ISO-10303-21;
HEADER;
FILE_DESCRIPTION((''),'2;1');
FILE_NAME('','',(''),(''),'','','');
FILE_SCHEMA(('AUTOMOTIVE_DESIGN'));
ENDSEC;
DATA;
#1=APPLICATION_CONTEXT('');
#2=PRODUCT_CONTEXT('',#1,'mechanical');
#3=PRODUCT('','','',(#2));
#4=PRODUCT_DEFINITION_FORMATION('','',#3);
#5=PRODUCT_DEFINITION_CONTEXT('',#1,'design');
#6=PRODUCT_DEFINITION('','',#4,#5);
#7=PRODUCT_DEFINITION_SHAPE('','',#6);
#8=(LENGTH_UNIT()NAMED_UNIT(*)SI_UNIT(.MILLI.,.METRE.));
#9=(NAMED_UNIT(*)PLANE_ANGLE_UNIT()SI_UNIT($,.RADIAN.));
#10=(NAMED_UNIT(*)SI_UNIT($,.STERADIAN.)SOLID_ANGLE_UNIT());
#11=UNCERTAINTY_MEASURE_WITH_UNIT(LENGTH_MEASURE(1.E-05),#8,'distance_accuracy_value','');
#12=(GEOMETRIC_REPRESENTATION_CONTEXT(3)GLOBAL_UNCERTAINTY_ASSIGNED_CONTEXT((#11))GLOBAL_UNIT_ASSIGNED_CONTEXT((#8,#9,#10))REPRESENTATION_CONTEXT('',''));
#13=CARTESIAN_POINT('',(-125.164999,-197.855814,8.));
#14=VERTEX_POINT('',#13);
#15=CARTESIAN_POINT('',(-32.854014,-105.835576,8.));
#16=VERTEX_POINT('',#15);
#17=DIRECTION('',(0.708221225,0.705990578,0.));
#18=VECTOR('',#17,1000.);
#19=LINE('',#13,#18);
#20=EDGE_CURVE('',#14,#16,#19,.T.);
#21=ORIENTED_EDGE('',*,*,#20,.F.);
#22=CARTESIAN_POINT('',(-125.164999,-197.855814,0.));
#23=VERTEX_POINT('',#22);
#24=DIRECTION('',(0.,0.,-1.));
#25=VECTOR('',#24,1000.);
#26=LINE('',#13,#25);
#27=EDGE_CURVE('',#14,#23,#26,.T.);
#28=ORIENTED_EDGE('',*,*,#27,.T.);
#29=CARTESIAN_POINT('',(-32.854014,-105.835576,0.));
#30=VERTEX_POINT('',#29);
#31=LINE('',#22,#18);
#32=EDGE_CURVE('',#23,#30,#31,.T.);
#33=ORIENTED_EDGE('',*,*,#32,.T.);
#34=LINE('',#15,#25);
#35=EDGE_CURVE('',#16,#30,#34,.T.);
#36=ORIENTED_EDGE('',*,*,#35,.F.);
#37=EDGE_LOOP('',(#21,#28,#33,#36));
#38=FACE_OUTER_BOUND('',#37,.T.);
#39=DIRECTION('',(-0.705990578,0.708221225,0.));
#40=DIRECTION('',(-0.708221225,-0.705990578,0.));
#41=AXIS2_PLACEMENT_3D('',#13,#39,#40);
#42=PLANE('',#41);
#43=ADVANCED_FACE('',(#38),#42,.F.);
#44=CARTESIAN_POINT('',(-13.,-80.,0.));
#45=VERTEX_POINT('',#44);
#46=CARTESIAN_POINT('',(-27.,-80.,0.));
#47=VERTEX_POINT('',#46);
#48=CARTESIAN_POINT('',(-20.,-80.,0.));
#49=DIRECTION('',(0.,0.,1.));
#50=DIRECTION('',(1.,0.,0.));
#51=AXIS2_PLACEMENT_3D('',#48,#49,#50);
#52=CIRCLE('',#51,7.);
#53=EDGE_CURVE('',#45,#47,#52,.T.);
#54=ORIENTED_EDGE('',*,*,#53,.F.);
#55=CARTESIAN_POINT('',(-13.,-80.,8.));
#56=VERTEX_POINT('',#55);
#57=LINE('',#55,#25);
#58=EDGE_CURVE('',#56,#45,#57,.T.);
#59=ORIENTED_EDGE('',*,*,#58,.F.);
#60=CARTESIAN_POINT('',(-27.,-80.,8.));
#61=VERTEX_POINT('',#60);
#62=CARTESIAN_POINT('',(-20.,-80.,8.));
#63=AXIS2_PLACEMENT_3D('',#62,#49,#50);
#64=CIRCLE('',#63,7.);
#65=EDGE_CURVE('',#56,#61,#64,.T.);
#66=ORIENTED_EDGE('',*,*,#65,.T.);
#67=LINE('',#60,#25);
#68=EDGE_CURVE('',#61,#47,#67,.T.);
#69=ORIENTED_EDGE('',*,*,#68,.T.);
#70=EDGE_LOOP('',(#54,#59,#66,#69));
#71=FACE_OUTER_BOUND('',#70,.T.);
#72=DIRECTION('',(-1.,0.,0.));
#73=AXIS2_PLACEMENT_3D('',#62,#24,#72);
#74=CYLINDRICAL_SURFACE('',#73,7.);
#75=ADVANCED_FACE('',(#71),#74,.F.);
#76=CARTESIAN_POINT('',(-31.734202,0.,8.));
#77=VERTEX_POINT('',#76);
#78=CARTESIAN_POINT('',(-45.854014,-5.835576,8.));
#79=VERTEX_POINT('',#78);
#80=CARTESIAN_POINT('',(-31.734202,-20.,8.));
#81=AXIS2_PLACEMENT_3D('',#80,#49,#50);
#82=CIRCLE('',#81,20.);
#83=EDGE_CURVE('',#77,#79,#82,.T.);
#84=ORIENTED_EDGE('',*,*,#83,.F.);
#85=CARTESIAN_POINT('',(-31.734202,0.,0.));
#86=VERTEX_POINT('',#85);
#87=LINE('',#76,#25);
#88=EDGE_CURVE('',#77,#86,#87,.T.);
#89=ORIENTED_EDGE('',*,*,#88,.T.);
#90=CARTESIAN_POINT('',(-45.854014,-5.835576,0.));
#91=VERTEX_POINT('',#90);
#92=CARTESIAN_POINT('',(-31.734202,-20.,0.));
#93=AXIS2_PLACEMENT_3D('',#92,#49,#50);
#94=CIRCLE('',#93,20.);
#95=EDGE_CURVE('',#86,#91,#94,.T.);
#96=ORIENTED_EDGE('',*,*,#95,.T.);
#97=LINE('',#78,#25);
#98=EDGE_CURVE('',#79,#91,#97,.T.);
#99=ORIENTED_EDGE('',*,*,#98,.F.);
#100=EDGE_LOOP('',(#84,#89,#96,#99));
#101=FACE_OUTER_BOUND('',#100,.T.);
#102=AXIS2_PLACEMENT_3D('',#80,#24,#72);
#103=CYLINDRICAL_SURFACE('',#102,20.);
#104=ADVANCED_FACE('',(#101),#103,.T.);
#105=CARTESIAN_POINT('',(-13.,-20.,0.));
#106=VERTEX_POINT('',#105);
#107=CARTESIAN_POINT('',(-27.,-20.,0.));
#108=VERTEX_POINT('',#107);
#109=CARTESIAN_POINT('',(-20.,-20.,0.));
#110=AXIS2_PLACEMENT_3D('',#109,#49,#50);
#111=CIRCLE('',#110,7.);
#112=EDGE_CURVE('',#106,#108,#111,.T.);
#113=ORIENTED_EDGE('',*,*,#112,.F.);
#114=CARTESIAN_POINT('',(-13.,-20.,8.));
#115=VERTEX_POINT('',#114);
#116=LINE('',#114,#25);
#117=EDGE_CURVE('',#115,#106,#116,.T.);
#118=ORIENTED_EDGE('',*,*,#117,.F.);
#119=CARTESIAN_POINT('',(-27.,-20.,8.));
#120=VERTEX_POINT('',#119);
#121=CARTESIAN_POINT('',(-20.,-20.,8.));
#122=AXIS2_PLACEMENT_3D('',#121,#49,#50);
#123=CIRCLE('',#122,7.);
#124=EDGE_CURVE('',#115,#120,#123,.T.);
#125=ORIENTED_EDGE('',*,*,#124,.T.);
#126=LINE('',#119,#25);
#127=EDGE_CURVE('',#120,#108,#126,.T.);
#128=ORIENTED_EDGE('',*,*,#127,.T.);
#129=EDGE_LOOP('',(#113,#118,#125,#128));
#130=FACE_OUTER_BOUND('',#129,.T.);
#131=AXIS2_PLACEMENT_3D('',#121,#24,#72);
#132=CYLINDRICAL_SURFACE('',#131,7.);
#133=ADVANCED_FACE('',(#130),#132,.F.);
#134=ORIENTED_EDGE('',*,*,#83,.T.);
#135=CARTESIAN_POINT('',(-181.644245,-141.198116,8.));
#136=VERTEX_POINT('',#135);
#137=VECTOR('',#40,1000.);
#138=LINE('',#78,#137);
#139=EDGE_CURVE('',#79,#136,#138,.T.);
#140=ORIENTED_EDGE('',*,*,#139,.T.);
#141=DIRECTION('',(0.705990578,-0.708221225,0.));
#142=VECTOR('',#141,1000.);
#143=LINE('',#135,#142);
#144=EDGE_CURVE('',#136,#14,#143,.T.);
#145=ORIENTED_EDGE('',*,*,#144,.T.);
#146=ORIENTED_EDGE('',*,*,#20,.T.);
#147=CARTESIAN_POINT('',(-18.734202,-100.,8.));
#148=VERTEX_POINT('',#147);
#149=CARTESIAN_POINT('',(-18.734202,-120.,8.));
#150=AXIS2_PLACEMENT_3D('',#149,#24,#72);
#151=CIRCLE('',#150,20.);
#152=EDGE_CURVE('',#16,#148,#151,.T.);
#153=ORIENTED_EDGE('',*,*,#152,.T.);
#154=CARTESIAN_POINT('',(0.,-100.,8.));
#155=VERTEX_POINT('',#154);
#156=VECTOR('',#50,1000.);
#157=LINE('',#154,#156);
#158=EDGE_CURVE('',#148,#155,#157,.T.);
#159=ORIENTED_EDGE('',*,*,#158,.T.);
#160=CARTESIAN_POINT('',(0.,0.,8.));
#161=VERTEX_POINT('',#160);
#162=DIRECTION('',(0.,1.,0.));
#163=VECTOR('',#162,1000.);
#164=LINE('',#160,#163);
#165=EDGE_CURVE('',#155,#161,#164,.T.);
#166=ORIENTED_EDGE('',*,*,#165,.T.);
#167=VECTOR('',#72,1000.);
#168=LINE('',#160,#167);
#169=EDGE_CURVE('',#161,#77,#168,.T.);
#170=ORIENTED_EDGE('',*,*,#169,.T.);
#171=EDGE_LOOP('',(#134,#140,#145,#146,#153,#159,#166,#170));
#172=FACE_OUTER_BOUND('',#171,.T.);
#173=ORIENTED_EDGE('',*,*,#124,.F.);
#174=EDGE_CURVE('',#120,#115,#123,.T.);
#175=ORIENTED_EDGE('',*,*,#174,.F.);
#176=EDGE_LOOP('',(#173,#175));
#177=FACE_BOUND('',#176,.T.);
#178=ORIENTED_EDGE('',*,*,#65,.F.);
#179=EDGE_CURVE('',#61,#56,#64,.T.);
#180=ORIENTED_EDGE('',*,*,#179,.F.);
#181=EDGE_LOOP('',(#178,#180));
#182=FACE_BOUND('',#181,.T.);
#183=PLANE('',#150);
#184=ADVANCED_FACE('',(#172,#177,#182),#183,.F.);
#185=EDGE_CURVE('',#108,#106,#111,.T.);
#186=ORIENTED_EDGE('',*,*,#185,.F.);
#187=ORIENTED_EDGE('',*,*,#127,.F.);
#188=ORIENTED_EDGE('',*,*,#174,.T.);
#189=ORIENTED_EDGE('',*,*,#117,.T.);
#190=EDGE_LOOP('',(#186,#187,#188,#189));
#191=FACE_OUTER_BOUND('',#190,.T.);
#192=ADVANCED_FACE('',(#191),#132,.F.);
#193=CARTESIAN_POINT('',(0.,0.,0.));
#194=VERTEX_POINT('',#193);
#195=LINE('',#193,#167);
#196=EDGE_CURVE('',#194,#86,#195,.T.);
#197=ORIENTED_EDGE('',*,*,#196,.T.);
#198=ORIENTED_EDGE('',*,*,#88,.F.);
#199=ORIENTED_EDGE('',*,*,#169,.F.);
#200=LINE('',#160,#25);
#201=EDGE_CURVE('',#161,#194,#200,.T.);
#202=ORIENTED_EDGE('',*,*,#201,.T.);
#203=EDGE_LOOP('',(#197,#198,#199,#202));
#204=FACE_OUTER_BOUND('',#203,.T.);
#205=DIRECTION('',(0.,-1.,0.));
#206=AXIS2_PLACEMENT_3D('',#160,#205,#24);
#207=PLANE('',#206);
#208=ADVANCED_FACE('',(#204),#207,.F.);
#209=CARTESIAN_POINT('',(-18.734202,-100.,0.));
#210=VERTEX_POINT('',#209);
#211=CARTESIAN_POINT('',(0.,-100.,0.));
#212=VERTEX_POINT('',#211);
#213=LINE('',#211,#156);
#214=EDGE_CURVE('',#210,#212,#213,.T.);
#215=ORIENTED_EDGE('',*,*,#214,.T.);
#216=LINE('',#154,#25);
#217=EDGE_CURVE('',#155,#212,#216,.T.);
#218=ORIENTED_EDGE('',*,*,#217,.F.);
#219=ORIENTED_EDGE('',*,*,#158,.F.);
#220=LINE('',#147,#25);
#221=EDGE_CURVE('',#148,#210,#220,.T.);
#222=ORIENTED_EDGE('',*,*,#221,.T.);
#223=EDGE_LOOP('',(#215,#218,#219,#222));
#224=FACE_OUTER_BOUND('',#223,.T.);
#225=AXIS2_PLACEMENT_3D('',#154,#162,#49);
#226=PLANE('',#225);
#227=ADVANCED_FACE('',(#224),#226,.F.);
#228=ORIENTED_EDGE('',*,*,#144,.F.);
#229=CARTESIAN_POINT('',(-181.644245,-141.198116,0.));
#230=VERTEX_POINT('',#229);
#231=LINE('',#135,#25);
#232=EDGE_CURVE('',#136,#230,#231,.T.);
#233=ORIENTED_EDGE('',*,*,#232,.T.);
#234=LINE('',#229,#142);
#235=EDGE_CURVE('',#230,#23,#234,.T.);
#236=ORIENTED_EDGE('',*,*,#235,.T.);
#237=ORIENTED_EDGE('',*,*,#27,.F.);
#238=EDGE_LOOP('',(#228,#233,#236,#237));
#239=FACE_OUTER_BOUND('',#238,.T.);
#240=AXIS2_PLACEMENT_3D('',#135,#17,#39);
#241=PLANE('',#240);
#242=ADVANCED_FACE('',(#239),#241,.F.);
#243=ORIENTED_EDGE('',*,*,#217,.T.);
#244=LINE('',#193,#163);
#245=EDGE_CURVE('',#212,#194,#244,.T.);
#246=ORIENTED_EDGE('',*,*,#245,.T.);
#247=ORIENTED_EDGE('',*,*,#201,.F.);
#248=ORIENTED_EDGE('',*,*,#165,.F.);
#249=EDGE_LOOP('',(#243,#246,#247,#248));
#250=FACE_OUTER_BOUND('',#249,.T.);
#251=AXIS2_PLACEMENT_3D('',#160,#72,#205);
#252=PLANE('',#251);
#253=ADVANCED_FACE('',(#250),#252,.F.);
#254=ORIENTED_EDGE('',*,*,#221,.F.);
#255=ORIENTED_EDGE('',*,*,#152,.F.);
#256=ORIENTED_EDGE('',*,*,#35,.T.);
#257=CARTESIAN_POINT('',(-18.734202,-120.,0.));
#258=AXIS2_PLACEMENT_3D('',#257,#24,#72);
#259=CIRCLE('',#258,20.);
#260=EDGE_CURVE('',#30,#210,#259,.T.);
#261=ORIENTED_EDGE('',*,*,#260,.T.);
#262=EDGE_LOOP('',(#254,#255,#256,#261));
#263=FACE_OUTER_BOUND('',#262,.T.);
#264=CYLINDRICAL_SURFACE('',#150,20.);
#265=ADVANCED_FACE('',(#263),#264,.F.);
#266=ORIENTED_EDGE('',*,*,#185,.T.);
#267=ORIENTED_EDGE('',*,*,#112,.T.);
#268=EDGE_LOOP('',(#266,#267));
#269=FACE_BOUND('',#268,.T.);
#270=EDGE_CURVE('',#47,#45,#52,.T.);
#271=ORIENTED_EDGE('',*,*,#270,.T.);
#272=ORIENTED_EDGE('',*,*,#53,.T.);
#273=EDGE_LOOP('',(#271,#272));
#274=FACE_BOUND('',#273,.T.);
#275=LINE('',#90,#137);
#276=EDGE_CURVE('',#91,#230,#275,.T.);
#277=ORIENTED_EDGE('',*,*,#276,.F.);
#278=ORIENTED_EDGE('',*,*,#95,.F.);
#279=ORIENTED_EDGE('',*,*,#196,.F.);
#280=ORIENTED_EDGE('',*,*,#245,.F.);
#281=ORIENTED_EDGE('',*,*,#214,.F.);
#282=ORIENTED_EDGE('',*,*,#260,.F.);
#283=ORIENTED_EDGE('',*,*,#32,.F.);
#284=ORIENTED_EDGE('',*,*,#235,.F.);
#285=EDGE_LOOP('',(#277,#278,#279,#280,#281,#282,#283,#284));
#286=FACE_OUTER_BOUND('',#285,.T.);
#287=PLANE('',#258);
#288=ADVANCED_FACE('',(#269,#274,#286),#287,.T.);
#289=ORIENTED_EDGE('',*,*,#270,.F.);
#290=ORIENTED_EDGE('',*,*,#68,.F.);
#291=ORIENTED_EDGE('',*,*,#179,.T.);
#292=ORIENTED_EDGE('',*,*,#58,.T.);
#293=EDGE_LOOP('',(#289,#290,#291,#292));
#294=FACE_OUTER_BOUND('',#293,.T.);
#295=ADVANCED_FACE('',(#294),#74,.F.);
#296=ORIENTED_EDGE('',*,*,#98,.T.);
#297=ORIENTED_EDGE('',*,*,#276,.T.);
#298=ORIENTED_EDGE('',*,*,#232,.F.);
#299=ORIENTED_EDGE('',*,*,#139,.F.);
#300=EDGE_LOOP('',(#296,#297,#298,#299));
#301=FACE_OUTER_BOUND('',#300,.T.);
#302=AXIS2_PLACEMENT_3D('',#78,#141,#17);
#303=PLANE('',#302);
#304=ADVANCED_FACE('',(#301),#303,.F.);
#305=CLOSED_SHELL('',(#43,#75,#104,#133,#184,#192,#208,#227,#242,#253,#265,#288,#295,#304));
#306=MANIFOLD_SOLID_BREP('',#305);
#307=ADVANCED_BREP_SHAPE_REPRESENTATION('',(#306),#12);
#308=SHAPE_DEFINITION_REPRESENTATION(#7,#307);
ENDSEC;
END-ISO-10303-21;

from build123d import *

# Parameters (mm, degrees)
SKETCH1_R           = 7
BOSS_EXTRUDE1_DEPTH = 8


with BuildPart() as part:
    # Sketch1 → Boss-Extrude1 (new body)
    with BuildSketch(Plane.XY):
        with BuildLine():
            Line((0, 0), (-31.73420201, 0))
            ThreePointArc((-31.73420201, 0), (-39.373295872, -1.516379008), (-45.854013577, -5.835575504))
            Line((-45.854013577, -5.835575504), (-181.644244963, -141.198115671))
            Line((-181.644244963, -141.198115671), (-125.164998695, -197.855813656))
            Line((-125.164998695, -197.855813656), (-32.854013577, -105.835575504))
            ThreePointArc((-32.854013577, -105.835575504), (-26.373295872, -101.516379008), (-18.73420201, -100))
            Line((-18.73420201, -100), (0, -100))
            Line((0, -100), (0, 0))
        make_face()
        with Locations((-20, -20)):
            Circle(SKETCH1_R, mode=Mode.SUBTRACT)
        with Locations((-20, -80)):
            Circle(SKETCH1_R, mode=Mode.SUBTRACT)
    extrude(amount=BOSS_EXTRUDE1_DEPTH)


solid = part.part
